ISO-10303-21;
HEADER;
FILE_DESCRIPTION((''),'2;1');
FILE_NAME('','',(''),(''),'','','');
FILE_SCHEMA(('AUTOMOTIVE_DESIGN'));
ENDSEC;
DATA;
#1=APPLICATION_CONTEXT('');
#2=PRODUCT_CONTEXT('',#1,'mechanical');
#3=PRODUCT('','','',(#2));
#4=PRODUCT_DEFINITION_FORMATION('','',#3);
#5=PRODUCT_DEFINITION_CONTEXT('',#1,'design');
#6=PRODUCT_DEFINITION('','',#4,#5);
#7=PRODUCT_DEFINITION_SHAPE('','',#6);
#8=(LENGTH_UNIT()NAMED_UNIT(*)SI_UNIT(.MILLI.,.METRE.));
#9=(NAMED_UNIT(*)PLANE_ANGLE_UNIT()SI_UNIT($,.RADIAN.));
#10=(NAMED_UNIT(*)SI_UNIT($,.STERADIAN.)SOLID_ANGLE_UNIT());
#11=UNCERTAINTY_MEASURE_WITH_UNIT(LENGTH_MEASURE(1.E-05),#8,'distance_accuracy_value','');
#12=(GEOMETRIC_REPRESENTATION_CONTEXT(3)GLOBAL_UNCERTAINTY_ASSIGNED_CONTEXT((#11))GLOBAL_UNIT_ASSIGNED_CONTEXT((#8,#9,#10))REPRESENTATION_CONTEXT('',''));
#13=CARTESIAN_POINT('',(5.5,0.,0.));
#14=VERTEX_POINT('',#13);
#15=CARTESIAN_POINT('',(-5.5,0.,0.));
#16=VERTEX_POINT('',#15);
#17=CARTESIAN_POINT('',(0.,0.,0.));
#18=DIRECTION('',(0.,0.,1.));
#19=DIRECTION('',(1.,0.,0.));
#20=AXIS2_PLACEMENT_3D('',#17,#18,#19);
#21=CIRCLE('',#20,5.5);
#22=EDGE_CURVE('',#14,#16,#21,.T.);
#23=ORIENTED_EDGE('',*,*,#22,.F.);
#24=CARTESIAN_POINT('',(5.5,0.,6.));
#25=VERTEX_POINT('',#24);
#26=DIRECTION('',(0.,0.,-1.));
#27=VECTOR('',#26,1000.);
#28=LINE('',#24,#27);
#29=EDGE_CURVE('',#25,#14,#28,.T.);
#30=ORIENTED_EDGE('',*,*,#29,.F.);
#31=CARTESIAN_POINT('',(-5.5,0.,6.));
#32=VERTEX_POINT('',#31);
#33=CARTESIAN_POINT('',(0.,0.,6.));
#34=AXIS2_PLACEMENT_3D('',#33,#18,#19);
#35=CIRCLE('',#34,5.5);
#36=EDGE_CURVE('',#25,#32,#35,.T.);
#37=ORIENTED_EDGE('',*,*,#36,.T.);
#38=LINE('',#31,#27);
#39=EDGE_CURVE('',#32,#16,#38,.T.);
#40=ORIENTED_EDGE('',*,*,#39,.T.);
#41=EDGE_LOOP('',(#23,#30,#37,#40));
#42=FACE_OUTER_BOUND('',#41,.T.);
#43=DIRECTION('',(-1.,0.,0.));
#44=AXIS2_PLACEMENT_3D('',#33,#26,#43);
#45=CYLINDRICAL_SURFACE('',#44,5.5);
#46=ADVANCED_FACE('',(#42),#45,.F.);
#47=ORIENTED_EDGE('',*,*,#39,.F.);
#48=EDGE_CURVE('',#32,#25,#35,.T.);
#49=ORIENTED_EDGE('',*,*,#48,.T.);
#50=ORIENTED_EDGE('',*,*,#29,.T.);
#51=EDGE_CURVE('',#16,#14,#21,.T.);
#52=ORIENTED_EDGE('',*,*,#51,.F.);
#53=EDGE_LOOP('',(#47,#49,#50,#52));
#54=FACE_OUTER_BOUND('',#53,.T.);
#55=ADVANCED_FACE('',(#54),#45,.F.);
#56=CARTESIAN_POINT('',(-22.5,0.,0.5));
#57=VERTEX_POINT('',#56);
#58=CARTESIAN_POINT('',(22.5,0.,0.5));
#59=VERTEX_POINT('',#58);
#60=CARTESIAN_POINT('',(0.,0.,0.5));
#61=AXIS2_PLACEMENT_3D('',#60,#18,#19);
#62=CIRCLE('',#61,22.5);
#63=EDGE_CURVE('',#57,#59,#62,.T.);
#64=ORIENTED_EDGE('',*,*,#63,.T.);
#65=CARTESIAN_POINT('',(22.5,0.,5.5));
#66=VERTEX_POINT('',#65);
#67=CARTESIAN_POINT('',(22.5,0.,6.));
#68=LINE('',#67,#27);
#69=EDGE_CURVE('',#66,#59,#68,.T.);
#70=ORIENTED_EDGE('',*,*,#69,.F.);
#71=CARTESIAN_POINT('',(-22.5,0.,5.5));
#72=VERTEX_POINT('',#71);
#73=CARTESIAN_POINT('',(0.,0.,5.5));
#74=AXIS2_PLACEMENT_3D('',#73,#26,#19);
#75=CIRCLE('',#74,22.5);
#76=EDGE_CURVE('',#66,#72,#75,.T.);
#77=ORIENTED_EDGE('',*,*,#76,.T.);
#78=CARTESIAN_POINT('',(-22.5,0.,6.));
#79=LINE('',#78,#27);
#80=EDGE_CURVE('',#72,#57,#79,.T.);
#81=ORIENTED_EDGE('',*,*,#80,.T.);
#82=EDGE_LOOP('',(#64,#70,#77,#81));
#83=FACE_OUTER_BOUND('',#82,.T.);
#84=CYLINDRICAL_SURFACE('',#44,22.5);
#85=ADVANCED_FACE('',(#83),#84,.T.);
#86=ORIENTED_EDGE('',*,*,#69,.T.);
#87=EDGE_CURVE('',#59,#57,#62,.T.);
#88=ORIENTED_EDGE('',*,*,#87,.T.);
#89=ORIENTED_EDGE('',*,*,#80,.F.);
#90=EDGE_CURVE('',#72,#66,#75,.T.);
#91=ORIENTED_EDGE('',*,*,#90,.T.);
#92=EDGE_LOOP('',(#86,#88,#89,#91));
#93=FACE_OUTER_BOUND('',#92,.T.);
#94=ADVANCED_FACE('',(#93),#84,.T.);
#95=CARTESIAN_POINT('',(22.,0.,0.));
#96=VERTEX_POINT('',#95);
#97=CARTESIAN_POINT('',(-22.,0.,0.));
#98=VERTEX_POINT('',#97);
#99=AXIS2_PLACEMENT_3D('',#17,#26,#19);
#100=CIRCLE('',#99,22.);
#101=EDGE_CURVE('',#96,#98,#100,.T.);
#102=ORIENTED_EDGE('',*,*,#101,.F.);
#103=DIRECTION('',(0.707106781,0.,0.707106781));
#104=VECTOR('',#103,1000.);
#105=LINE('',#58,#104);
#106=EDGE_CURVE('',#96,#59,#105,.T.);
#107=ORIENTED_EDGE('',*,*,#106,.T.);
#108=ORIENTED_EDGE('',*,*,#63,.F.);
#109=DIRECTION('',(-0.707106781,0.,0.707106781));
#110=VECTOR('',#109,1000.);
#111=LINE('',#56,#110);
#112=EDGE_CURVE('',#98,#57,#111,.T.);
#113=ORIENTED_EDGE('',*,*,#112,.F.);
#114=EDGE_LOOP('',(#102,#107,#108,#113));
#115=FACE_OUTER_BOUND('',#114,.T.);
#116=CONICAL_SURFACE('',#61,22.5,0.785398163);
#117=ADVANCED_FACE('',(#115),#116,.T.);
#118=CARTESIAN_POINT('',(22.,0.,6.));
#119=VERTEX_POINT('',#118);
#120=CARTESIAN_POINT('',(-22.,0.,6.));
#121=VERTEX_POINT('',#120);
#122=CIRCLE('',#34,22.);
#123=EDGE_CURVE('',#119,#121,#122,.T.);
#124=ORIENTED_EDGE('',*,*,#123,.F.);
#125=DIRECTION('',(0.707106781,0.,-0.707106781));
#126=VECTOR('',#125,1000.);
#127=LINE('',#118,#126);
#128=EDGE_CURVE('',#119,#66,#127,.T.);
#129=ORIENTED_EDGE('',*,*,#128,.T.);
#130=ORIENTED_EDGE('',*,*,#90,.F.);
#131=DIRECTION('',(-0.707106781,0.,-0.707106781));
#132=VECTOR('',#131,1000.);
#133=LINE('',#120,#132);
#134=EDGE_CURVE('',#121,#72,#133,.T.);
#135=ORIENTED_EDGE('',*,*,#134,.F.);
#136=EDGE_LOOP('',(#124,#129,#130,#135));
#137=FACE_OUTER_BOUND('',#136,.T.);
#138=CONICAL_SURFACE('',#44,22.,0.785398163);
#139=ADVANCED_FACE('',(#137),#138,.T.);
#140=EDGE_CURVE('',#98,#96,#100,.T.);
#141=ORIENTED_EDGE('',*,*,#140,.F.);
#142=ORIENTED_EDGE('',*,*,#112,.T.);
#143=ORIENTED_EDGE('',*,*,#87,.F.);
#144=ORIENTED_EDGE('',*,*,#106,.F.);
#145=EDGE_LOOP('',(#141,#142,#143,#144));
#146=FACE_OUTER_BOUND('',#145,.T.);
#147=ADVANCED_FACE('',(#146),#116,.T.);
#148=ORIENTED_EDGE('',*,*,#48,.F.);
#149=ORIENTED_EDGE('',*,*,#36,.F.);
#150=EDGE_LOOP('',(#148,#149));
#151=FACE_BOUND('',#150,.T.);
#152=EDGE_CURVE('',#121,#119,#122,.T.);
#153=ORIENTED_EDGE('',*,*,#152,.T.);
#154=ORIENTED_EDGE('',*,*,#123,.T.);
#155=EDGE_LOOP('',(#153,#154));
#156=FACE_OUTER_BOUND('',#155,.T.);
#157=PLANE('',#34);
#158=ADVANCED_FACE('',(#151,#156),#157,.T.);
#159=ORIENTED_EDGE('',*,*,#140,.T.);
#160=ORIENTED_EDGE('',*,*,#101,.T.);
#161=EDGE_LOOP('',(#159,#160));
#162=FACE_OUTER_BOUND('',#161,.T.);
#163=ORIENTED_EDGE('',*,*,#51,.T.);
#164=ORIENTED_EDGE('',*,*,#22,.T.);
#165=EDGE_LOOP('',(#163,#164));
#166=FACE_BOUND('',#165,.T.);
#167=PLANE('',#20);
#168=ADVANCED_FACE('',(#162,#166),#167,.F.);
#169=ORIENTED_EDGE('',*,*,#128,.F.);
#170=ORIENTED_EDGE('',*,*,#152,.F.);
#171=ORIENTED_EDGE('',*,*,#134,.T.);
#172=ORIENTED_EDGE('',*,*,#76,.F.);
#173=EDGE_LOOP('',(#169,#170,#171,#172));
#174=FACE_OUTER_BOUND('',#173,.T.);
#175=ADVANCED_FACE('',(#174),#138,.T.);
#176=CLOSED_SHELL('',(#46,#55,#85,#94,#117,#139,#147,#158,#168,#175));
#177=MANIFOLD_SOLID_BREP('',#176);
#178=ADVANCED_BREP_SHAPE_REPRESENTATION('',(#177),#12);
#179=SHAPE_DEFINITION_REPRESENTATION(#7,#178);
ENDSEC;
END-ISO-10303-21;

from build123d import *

# Parameters (mm, degrees)
SKETCH_1_R      = 22.5
SKETCH_1_R_2    = 5.5
EXTRUDE_1_DEPTH = 6
CHAMFER_1_SIZE  = 0.5


with BuildPart() as part:
    # 草图1 → 凸台-拉伸1 (new body)
    with BuildSketch(Plane.XY):
        Circle(SKETCH_1_R)
        Circle(SKETCH_1_R_2, mode=Mode.SUBTRACT)
    extrude(amount=EXTRUDE_1_DEPTH)

    # 倒角1
    chamfer_1_edges = [part.edges().sort_by_distance(p)[0] for p in [
        (-22.5, 0, 0),
        (-22.5, 0, 6),
    ]]
    chamfer(chamfer_1_edges, length=CHAMFER_1_SIZE)


solid = part.part
